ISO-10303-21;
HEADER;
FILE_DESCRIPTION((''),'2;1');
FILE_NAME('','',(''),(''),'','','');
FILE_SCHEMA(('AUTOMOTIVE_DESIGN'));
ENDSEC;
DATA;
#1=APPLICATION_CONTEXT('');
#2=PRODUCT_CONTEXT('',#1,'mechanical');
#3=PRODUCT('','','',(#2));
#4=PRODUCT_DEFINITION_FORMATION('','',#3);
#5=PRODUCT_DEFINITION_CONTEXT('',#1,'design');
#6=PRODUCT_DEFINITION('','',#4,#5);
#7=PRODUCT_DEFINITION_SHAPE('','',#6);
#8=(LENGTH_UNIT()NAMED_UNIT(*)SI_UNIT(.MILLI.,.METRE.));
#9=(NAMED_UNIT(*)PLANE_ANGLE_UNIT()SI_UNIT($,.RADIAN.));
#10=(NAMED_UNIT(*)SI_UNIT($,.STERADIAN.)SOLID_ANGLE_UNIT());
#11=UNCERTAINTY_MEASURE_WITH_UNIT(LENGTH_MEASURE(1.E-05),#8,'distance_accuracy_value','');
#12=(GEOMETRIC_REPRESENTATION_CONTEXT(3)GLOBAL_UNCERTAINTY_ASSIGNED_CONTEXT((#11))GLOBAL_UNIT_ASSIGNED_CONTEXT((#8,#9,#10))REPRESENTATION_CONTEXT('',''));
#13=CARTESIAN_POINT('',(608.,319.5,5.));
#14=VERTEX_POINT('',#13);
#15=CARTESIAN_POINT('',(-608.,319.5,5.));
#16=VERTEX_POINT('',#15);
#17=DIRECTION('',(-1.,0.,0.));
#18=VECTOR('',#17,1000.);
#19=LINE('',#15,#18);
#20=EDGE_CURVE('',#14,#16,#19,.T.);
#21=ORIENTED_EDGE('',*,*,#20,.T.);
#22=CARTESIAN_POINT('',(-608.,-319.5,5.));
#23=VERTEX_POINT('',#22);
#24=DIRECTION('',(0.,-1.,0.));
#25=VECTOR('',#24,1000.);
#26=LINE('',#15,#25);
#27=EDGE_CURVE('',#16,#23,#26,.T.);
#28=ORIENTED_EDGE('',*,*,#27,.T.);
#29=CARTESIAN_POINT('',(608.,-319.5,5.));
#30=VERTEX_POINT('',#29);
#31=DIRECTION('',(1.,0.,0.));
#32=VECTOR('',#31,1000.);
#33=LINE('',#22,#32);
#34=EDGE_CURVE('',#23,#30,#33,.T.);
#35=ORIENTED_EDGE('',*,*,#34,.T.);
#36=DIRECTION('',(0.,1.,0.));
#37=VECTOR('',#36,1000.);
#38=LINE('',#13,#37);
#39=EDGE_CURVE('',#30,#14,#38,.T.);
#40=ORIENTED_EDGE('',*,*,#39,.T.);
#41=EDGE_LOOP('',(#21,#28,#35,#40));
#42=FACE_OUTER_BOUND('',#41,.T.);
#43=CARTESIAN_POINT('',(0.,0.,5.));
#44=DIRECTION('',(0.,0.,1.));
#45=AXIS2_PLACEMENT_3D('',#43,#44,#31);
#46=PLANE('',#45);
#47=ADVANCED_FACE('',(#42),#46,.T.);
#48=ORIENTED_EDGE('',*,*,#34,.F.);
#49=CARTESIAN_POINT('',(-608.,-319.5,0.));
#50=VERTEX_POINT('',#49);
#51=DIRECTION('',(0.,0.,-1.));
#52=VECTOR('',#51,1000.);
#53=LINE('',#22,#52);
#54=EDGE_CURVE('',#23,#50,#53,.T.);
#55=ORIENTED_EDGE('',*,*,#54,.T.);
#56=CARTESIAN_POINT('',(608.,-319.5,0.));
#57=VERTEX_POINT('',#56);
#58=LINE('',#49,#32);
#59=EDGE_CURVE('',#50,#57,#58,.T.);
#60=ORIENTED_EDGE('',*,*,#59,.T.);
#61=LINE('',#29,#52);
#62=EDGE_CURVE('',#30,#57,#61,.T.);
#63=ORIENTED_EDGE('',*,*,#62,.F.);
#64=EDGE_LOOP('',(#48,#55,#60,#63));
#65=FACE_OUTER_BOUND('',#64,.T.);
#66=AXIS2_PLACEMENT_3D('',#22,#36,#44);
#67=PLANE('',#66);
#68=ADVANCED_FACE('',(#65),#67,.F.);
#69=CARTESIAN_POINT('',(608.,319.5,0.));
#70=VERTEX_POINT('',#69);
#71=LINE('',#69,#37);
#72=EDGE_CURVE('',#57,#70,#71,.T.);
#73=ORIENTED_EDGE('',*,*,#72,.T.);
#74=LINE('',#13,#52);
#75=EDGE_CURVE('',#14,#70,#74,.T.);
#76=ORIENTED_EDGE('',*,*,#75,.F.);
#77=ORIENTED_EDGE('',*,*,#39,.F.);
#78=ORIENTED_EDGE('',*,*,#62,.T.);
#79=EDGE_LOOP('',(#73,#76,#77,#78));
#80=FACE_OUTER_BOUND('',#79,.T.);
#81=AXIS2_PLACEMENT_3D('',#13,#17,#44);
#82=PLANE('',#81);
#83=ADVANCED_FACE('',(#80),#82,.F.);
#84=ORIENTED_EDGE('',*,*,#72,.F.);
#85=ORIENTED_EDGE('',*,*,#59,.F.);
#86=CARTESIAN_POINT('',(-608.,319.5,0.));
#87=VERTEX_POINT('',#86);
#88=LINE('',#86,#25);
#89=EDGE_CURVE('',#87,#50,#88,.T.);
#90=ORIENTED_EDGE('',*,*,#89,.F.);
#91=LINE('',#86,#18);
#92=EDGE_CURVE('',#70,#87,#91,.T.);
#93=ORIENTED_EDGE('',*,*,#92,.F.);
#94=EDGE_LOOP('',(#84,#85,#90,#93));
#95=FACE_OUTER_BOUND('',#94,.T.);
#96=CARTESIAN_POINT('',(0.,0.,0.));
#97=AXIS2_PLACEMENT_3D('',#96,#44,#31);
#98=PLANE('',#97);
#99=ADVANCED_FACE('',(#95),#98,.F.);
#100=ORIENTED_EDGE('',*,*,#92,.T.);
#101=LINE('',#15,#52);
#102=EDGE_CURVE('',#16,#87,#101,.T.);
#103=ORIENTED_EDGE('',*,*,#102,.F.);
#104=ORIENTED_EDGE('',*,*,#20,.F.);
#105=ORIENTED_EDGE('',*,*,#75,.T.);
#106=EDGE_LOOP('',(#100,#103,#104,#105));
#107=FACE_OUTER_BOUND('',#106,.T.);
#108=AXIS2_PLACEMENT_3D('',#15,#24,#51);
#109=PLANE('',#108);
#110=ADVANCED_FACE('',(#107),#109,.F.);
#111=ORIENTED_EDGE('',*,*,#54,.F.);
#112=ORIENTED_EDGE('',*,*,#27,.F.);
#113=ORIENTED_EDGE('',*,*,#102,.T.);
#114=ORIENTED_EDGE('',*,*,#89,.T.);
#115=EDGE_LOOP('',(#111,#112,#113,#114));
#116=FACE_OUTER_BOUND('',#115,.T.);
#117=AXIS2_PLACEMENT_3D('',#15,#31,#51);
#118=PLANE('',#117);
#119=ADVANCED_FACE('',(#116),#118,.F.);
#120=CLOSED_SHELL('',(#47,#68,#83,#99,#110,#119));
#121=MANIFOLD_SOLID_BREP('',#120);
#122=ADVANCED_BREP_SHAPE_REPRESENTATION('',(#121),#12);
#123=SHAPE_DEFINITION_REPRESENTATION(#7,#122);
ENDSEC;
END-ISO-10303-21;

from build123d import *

# Parameters (mm, degrees)
SKETCH_1_W      = 1216
SKETCH_1_H      = 639
EXTRUDE_1_DEPTH = 5


with BuildPart() as part:
    # 草图1 → 凸台-拉伸1 (new body)
    with BuildSketch(Plane.XY):
        Rectangle(SKETCH_1_W, SKETCH_1_H)
    extrude(amount=EXTRUDE_1_DEPTH)


solid = part.part
